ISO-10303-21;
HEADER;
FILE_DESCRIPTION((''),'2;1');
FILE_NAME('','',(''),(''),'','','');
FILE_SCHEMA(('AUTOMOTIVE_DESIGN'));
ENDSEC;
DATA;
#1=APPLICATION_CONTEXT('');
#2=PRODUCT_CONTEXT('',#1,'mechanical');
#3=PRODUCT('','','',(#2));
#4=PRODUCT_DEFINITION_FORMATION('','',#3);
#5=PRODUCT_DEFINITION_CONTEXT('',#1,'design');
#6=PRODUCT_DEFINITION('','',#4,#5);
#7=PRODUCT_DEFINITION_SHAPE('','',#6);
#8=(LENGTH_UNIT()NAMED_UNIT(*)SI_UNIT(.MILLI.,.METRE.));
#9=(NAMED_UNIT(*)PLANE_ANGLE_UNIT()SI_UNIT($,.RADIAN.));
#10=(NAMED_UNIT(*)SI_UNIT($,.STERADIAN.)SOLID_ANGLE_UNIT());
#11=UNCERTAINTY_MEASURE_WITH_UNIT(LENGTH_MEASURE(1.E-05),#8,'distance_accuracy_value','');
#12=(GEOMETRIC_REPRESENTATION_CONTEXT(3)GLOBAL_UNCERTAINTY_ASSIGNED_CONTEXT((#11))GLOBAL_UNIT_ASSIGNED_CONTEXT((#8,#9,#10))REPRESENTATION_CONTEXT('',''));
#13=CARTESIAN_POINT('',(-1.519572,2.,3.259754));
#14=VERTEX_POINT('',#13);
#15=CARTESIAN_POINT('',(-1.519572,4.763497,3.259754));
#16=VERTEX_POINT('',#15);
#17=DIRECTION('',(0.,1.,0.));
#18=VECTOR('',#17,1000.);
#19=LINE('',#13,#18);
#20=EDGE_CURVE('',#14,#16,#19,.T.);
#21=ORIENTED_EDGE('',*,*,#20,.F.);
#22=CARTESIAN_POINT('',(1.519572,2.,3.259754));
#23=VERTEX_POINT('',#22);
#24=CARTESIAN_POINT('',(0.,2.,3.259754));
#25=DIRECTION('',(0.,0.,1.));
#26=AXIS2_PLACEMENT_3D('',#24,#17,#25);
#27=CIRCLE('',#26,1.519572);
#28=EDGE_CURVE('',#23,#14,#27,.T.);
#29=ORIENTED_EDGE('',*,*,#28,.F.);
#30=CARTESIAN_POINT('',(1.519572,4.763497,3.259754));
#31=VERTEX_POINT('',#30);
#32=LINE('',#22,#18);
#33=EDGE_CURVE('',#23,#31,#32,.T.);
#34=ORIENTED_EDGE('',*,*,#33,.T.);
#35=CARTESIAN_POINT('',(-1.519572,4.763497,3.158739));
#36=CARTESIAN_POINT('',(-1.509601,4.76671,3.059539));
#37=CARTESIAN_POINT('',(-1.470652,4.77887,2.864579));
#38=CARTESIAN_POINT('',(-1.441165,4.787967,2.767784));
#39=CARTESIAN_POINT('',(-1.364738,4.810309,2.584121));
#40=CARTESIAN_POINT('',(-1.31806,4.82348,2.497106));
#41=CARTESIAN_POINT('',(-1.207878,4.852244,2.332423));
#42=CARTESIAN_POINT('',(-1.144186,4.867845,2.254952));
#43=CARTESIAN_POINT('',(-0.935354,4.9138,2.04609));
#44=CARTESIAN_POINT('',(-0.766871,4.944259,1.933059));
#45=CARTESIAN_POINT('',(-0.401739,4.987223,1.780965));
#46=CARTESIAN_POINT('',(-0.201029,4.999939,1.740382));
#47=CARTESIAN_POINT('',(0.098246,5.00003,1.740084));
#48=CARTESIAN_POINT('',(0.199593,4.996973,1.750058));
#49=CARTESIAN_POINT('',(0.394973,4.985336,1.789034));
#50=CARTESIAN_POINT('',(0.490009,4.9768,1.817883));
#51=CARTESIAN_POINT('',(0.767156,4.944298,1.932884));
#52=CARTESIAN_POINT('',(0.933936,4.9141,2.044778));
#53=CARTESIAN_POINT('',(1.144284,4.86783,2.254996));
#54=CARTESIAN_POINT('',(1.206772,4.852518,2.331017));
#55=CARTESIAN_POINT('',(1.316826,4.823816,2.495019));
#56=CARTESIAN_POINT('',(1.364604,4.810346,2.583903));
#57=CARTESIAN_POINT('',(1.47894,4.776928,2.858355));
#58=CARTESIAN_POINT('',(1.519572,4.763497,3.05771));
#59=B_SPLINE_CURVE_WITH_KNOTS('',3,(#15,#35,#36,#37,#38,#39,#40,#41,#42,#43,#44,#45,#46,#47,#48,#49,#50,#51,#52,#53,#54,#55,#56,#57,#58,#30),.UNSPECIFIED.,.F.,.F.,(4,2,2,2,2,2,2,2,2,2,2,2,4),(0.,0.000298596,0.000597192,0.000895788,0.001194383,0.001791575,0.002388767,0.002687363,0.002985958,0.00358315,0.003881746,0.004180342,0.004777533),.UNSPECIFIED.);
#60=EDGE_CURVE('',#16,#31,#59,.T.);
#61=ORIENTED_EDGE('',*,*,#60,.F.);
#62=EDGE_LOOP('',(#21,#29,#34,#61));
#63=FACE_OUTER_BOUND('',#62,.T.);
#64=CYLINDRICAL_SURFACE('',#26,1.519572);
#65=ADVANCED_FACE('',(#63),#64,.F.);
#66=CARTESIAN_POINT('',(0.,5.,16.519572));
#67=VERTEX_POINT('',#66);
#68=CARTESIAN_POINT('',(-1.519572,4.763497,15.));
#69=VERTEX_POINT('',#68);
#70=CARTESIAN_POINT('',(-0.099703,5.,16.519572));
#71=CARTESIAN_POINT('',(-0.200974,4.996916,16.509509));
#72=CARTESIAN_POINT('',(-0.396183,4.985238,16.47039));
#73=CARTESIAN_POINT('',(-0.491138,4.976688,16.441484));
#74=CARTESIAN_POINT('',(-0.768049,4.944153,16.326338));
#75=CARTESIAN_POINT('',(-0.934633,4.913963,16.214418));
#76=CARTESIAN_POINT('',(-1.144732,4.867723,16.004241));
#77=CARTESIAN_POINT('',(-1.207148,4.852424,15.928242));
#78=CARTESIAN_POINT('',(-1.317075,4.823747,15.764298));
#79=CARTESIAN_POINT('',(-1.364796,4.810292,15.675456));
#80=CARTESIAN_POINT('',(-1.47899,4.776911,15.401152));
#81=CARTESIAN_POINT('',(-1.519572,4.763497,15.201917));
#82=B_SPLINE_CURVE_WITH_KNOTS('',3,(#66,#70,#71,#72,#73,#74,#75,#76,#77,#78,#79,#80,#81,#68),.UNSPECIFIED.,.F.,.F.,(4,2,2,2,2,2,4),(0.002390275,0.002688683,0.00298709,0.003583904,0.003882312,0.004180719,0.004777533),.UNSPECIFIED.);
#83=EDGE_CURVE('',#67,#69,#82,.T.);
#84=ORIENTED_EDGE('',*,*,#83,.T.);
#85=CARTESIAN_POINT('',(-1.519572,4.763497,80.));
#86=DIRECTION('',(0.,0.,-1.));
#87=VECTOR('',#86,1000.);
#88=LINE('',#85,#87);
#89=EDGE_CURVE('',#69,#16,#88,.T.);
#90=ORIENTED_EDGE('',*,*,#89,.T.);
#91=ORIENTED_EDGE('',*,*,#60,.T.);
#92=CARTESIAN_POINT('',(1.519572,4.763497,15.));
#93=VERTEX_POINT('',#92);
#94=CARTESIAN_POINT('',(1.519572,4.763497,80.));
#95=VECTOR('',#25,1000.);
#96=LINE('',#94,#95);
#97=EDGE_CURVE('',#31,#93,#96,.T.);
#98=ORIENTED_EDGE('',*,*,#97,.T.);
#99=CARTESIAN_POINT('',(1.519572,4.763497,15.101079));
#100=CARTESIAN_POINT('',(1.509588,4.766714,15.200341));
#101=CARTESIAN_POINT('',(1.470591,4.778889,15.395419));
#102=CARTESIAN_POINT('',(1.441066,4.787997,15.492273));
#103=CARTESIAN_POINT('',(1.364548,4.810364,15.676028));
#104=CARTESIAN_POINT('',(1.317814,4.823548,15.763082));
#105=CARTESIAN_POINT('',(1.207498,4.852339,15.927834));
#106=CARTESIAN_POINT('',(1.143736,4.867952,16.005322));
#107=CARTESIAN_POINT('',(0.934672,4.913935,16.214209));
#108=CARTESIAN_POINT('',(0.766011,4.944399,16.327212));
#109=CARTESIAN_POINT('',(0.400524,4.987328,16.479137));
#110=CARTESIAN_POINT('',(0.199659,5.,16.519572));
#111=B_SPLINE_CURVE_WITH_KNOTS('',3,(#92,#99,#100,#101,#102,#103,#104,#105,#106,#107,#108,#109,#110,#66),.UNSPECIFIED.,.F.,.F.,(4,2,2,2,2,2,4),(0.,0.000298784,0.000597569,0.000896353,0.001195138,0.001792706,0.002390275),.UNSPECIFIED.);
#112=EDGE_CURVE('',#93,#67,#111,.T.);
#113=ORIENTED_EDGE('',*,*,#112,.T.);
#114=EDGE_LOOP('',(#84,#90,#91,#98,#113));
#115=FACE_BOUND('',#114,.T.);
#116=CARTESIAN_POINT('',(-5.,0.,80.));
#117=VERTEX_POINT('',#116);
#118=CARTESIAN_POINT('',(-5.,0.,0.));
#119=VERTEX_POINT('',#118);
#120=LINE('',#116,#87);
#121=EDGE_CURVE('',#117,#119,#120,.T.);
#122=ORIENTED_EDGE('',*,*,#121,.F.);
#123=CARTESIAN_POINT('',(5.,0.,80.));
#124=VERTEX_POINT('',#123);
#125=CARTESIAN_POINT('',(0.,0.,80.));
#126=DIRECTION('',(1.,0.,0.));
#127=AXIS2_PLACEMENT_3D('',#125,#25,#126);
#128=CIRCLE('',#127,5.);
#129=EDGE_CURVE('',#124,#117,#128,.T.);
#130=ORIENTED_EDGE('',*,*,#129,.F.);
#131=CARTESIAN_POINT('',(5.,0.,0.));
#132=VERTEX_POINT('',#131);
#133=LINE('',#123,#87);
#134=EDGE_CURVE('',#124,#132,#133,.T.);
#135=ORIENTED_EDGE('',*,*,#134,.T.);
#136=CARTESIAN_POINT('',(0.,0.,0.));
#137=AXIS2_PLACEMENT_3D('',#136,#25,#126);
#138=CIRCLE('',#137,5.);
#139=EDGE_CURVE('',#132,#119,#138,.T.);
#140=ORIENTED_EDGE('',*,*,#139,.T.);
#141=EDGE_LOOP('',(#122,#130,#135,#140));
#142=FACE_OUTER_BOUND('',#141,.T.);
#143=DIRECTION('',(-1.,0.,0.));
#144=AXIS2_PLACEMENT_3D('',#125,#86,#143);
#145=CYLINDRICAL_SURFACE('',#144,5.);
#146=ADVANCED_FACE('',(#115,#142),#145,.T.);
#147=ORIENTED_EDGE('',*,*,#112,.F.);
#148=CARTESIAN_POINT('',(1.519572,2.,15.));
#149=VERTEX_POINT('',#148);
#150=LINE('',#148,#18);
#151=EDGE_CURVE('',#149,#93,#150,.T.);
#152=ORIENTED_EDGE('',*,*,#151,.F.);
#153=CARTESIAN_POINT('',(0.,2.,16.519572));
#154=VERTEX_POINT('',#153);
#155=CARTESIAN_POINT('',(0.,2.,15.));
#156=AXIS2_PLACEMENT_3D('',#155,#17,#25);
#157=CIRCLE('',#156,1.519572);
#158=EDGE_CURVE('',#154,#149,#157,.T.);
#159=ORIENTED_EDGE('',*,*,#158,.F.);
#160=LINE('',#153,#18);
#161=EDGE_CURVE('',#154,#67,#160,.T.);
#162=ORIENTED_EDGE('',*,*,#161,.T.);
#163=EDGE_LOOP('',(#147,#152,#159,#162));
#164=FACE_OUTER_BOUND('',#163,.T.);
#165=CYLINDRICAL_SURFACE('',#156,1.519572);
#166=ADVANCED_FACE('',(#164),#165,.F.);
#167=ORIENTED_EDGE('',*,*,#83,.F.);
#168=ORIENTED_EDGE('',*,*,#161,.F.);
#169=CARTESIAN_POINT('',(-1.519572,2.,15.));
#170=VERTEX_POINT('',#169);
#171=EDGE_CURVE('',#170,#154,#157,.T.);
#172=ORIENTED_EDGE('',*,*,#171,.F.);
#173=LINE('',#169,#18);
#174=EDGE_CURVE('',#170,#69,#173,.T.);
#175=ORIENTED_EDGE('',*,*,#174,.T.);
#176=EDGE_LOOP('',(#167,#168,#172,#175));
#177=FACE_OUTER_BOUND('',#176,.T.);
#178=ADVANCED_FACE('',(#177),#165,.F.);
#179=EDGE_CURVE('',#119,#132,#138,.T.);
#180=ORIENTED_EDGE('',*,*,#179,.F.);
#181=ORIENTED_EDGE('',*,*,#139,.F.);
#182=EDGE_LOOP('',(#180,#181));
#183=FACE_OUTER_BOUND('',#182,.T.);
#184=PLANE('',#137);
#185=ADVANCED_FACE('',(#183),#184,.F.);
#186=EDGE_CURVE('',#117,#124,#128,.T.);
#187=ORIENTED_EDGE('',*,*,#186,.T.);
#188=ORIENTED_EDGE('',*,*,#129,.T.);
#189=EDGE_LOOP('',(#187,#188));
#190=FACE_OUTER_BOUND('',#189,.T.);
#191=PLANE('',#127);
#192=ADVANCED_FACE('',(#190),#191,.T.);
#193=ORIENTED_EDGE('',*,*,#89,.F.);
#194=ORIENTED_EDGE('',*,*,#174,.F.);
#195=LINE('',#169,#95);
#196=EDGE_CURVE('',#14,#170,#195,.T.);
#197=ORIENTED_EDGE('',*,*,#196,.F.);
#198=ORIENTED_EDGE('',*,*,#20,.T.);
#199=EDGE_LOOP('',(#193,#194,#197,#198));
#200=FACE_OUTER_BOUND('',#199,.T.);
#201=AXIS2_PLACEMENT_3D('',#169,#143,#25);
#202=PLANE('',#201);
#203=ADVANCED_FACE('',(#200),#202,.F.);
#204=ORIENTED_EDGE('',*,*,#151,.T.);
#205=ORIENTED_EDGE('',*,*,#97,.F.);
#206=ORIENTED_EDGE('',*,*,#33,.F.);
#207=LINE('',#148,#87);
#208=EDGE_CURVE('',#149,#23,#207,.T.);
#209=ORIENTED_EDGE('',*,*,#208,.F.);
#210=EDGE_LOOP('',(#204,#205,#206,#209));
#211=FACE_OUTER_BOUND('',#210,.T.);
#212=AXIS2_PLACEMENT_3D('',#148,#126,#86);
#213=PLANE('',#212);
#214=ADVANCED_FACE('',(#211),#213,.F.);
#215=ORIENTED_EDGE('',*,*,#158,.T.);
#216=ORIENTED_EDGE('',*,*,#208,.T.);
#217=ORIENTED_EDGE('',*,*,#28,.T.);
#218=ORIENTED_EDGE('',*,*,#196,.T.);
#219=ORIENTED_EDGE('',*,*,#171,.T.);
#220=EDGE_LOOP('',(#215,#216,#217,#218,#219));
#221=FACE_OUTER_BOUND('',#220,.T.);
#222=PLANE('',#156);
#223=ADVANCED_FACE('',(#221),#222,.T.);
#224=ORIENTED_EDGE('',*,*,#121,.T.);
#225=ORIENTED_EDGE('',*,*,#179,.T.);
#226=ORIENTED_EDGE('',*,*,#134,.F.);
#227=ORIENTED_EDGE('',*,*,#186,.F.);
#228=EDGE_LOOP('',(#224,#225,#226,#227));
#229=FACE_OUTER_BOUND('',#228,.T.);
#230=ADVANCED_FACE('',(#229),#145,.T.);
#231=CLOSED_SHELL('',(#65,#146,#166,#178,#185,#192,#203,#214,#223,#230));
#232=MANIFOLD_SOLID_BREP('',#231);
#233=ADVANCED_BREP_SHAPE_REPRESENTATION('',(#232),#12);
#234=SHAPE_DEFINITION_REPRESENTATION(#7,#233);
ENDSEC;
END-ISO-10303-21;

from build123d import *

# Parameters (mm, degrees)
SKETCH1_R           = 5
BOSS_EXTRUDE1_DEPTH = 80
CUT_EXTRUDE2_DEPTH  = 3


with BuildPart() as part:
    # Sketch1 → Boss-Extrude1 (new body)
    with BuildSketch(Plane.XY):
        Circle(SKETCH1_R)
    extrude(amount=BOSS_EXTRUDE1_DEPTH)

    # Sketch2 → Cut-Extrude2 (cut)
    with BuildSketch(Plane(origin=(0, 5, 0), x_dir=(1, 0, 0), z_dir=(0, 1, 0))):
        with BuildLine():
            Line((-1.519571935, -15), (-1.519571935, -3.259754454))
            ThreePointArc((-1.519571935, -3.259754454), (0, -1.740182518), (1.519571935, -3.259754454))
            Line((1.519571935, -3.259754454), (1.519571935, -15))
            ThreePointArc((1.519571935, -15), (0, -16.519571935), (-1.519571935, -15))
        make_face()
    extrude(amount=-CUT_EXTRUDE2_DEPTH, mode=Mode.SUBTRACT)


solid = part.part
